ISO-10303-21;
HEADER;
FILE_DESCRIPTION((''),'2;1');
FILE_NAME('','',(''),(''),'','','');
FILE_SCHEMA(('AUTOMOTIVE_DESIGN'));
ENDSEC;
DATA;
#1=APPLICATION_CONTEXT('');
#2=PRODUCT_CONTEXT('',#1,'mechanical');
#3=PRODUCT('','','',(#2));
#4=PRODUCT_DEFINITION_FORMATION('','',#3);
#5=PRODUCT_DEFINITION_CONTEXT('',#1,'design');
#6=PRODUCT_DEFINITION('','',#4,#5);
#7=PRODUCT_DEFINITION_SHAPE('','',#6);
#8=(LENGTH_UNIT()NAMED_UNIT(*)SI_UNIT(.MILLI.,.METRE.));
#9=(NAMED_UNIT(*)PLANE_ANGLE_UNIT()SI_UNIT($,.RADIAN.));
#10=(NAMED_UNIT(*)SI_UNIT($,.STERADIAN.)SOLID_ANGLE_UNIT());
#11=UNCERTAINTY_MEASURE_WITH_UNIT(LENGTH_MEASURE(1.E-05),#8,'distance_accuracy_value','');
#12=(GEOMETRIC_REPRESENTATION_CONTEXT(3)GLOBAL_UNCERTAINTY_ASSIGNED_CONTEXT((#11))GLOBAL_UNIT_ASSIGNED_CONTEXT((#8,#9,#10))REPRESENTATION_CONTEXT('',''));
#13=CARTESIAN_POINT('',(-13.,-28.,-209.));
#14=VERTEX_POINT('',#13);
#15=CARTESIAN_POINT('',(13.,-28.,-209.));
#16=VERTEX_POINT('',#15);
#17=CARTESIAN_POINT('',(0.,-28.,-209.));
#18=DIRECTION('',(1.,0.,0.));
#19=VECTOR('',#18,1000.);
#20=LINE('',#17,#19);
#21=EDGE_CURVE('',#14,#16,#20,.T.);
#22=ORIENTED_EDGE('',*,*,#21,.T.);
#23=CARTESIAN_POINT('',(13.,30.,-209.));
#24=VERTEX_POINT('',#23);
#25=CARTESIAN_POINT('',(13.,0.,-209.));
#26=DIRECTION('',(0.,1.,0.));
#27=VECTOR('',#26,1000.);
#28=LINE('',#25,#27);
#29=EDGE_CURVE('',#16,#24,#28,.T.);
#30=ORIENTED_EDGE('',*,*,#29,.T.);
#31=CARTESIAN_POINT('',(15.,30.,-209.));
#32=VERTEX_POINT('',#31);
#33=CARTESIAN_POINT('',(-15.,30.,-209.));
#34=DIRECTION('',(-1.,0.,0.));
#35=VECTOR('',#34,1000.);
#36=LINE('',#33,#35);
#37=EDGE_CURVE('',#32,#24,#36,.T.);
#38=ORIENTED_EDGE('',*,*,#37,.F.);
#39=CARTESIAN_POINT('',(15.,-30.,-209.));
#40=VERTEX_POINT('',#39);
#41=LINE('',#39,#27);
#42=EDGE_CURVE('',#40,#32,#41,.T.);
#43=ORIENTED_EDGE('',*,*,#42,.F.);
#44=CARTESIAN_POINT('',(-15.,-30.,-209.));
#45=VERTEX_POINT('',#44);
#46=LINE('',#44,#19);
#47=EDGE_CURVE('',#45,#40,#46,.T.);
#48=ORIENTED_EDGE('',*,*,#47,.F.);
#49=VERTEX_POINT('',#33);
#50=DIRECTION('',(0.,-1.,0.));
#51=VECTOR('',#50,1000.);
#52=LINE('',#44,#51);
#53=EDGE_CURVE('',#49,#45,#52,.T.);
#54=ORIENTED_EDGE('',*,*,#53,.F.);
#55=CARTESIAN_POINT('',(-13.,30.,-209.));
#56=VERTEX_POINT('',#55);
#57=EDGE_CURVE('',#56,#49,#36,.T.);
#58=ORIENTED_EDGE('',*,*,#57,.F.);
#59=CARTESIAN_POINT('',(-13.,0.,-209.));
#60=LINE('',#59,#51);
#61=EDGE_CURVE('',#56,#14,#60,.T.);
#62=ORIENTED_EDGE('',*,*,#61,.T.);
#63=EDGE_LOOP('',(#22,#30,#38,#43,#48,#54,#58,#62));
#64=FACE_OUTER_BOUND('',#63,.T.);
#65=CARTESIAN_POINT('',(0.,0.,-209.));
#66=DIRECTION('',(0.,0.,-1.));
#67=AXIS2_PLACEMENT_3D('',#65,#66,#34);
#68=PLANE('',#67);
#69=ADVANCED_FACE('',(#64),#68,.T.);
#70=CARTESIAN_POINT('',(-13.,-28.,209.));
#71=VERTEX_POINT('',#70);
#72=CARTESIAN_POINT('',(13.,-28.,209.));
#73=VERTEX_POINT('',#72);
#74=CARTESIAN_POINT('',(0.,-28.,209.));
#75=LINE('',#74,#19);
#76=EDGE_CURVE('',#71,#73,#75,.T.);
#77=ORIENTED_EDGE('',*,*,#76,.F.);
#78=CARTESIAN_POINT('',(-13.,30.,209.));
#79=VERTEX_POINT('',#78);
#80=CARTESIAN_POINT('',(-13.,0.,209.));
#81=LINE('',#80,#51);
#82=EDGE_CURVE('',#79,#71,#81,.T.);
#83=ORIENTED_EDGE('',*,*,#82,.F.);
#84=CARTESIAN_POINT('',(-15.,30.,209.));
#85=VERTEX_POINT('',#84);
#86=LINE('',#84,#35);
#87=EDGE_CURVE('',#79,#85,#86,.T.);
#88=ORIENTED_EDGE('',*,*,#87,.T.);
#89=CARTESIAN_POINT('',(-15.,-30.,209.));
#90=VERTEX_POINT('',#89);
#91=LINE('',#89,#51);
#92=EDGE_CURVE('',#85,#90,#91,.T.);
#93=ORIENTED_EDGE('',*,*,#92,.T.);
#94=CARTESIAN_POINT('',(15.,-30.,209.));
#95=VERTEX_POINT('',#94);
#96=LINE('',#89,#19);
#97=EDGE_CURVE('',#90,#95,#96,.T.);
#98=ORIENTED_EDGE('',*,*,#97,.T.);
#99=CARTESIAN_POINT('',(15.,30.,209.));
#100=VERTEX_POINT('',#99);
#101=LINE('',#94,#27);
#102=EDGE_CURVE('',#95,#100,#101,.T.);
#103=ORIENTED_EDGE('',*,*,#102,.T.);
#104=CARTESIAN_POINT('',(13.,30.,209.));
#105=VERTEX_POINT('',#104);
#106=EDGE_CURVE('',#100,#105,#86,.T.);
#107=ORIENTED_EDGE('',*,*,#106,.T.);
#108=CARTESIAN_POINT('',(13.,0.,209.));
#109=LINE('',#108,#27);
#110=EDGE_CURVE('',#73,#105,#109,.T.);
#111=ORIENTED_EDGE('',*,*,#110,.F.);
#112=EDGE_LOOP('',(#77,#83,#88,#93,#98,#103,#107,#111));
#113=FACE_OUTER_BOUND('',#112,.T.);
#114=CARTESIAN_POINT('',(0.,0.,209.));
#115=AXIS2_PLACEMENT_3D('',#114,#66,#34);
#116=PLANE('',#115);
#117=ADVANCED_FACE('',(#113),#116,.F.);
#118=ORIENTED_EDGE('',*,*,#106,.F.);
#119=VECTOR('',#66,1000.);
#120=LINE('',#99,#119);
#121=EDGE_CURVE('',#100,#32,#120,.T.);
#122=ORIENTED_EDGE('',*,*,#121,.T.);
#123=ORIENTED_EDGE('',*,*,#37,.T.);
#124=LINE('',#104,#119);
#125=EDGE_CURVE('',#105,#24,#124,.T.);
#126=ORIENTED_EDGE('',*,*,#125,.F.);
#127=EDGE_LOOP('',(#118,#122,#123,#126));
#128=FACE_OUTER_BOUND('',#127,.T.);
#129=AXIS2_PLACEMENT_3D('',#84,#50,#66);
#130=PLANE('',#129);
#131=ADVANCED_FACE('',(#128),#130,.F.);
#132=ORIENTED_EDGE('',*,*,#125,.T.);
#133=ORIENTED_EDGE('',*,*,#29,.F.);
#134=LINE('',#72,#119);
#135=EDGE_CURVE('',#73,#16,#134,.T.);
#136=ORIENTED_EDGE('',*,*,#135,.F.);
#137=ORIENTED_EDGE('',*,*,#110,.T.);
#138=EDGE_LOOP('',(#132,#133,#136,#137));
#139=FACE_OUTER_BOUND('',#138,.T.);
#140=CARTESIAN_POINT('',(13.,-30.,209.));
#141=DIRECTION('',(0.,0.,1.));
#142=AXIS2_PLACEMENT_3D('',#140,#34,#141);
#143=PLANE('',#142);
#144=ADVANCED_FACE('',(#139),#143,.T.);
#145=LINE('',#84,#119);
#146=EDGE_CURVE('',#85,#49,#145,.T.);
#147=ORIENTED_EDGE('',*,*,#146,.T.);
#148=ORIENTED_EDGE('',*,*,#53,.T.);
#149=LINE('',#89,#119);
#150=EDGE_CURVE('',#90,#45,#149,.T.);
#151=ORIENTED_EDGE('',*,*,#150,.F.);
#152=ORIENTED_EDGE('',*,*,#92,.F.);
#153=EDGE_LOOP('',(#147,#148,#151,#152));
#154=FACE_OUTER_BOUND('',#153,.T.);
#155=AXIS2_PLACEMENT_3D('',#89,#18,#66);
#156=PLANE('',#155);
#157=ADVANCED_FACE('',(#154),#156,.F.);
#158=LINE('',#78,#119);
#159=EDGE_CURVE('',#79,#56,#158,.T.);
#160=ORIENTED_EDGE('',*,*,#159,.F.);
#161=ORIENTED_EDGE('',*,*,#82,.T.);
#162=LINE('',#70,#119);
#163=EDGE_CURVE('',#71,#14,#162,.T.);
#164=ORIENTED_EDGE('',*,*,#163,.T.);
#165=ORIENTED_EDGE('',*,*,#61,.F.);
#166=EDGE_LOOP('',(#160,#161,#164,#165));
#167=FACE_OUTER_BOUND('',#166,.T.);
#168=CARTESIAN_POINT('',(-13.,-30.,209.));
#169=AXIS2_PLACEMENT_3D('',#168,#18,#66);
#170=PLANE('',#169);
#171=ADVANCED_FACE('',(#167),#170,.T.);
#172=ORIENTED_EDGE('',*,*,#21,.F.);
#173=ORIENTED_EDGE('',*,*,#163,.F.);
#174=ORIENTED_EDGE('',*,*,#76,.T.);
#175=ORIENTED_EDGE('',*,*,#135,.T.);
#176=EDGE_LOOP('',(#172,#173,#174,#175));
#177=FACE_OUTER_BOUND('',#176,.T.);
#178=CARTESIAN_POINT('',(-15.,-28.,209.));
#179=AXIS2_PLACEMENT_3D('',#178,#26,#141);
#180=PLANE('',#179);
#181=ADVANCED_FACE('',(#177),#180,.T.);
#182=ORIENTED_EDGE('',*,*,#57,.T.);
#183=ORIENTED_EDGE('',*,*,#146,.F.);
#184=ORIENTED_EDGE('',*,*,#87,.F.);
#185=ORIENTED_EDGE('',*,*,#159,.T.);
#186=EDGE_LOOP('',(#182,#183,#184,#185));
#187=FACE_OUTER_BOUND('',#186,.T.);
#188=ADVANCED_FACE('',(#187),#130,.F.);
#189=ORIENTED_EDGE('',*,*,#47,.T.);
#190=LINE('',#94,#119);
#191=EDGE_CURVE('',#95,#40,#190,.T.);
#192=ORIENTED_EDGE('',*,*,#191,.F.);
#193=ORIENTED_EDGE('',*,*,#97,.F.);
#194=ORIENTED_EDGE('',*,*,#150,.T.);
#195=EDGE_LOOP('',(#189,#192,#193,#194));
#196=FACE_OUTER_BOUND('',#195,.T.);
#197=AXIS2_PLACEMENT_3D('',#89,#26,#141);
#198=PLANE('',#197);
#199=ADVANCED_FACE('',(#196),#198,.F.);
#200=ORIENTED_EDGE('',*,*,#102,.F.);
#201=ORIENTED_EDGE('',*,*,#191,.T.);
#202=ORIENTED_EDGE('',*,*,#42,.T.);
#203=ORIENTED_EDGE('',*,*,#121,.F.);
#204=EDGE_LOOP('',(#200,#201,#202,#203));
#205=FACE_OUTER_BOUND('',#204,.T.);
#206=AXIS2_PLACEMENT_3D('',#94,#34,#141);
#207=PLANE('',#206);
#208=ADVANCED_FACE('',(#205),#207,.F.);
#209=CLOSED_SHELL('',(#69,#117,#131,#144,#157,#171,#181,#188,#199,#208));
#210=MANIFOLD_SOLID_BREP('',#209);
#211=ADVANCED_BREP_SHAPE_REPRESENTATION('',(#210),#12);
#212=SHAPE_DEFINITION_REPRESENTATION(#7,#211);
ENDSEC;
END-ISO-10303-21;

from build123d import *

# Parameters (mm, degrees)
SKETCH_1_W      = 30
SKETCH_1_H      = 60
EXTRUDE_1_DEPTH = 209
SHELL_1_T       = -2


with BuildPart() as part:
    # 草图1 → 凸台-拉伸1 (new, symmetric)
    with BuildSketch(Plane.XY):
        Rectangle(SKETCH_1_W, SKETCH_1_H)
    extrude(amount=EXTRUDE_1_DEPTH, both=True)

    # 抽壳1
    shell_1_openings = [part.faces().sort_by_distance(p)[0] for p in [
        (0, 0, 209),
        (0, 0, -209),
        (0, 30, 0),
    ]]
    offset(amount=SHELL_1_T, openings=shell_1_openings, kind=Kind.INTERSECTION)


solid = part.part
